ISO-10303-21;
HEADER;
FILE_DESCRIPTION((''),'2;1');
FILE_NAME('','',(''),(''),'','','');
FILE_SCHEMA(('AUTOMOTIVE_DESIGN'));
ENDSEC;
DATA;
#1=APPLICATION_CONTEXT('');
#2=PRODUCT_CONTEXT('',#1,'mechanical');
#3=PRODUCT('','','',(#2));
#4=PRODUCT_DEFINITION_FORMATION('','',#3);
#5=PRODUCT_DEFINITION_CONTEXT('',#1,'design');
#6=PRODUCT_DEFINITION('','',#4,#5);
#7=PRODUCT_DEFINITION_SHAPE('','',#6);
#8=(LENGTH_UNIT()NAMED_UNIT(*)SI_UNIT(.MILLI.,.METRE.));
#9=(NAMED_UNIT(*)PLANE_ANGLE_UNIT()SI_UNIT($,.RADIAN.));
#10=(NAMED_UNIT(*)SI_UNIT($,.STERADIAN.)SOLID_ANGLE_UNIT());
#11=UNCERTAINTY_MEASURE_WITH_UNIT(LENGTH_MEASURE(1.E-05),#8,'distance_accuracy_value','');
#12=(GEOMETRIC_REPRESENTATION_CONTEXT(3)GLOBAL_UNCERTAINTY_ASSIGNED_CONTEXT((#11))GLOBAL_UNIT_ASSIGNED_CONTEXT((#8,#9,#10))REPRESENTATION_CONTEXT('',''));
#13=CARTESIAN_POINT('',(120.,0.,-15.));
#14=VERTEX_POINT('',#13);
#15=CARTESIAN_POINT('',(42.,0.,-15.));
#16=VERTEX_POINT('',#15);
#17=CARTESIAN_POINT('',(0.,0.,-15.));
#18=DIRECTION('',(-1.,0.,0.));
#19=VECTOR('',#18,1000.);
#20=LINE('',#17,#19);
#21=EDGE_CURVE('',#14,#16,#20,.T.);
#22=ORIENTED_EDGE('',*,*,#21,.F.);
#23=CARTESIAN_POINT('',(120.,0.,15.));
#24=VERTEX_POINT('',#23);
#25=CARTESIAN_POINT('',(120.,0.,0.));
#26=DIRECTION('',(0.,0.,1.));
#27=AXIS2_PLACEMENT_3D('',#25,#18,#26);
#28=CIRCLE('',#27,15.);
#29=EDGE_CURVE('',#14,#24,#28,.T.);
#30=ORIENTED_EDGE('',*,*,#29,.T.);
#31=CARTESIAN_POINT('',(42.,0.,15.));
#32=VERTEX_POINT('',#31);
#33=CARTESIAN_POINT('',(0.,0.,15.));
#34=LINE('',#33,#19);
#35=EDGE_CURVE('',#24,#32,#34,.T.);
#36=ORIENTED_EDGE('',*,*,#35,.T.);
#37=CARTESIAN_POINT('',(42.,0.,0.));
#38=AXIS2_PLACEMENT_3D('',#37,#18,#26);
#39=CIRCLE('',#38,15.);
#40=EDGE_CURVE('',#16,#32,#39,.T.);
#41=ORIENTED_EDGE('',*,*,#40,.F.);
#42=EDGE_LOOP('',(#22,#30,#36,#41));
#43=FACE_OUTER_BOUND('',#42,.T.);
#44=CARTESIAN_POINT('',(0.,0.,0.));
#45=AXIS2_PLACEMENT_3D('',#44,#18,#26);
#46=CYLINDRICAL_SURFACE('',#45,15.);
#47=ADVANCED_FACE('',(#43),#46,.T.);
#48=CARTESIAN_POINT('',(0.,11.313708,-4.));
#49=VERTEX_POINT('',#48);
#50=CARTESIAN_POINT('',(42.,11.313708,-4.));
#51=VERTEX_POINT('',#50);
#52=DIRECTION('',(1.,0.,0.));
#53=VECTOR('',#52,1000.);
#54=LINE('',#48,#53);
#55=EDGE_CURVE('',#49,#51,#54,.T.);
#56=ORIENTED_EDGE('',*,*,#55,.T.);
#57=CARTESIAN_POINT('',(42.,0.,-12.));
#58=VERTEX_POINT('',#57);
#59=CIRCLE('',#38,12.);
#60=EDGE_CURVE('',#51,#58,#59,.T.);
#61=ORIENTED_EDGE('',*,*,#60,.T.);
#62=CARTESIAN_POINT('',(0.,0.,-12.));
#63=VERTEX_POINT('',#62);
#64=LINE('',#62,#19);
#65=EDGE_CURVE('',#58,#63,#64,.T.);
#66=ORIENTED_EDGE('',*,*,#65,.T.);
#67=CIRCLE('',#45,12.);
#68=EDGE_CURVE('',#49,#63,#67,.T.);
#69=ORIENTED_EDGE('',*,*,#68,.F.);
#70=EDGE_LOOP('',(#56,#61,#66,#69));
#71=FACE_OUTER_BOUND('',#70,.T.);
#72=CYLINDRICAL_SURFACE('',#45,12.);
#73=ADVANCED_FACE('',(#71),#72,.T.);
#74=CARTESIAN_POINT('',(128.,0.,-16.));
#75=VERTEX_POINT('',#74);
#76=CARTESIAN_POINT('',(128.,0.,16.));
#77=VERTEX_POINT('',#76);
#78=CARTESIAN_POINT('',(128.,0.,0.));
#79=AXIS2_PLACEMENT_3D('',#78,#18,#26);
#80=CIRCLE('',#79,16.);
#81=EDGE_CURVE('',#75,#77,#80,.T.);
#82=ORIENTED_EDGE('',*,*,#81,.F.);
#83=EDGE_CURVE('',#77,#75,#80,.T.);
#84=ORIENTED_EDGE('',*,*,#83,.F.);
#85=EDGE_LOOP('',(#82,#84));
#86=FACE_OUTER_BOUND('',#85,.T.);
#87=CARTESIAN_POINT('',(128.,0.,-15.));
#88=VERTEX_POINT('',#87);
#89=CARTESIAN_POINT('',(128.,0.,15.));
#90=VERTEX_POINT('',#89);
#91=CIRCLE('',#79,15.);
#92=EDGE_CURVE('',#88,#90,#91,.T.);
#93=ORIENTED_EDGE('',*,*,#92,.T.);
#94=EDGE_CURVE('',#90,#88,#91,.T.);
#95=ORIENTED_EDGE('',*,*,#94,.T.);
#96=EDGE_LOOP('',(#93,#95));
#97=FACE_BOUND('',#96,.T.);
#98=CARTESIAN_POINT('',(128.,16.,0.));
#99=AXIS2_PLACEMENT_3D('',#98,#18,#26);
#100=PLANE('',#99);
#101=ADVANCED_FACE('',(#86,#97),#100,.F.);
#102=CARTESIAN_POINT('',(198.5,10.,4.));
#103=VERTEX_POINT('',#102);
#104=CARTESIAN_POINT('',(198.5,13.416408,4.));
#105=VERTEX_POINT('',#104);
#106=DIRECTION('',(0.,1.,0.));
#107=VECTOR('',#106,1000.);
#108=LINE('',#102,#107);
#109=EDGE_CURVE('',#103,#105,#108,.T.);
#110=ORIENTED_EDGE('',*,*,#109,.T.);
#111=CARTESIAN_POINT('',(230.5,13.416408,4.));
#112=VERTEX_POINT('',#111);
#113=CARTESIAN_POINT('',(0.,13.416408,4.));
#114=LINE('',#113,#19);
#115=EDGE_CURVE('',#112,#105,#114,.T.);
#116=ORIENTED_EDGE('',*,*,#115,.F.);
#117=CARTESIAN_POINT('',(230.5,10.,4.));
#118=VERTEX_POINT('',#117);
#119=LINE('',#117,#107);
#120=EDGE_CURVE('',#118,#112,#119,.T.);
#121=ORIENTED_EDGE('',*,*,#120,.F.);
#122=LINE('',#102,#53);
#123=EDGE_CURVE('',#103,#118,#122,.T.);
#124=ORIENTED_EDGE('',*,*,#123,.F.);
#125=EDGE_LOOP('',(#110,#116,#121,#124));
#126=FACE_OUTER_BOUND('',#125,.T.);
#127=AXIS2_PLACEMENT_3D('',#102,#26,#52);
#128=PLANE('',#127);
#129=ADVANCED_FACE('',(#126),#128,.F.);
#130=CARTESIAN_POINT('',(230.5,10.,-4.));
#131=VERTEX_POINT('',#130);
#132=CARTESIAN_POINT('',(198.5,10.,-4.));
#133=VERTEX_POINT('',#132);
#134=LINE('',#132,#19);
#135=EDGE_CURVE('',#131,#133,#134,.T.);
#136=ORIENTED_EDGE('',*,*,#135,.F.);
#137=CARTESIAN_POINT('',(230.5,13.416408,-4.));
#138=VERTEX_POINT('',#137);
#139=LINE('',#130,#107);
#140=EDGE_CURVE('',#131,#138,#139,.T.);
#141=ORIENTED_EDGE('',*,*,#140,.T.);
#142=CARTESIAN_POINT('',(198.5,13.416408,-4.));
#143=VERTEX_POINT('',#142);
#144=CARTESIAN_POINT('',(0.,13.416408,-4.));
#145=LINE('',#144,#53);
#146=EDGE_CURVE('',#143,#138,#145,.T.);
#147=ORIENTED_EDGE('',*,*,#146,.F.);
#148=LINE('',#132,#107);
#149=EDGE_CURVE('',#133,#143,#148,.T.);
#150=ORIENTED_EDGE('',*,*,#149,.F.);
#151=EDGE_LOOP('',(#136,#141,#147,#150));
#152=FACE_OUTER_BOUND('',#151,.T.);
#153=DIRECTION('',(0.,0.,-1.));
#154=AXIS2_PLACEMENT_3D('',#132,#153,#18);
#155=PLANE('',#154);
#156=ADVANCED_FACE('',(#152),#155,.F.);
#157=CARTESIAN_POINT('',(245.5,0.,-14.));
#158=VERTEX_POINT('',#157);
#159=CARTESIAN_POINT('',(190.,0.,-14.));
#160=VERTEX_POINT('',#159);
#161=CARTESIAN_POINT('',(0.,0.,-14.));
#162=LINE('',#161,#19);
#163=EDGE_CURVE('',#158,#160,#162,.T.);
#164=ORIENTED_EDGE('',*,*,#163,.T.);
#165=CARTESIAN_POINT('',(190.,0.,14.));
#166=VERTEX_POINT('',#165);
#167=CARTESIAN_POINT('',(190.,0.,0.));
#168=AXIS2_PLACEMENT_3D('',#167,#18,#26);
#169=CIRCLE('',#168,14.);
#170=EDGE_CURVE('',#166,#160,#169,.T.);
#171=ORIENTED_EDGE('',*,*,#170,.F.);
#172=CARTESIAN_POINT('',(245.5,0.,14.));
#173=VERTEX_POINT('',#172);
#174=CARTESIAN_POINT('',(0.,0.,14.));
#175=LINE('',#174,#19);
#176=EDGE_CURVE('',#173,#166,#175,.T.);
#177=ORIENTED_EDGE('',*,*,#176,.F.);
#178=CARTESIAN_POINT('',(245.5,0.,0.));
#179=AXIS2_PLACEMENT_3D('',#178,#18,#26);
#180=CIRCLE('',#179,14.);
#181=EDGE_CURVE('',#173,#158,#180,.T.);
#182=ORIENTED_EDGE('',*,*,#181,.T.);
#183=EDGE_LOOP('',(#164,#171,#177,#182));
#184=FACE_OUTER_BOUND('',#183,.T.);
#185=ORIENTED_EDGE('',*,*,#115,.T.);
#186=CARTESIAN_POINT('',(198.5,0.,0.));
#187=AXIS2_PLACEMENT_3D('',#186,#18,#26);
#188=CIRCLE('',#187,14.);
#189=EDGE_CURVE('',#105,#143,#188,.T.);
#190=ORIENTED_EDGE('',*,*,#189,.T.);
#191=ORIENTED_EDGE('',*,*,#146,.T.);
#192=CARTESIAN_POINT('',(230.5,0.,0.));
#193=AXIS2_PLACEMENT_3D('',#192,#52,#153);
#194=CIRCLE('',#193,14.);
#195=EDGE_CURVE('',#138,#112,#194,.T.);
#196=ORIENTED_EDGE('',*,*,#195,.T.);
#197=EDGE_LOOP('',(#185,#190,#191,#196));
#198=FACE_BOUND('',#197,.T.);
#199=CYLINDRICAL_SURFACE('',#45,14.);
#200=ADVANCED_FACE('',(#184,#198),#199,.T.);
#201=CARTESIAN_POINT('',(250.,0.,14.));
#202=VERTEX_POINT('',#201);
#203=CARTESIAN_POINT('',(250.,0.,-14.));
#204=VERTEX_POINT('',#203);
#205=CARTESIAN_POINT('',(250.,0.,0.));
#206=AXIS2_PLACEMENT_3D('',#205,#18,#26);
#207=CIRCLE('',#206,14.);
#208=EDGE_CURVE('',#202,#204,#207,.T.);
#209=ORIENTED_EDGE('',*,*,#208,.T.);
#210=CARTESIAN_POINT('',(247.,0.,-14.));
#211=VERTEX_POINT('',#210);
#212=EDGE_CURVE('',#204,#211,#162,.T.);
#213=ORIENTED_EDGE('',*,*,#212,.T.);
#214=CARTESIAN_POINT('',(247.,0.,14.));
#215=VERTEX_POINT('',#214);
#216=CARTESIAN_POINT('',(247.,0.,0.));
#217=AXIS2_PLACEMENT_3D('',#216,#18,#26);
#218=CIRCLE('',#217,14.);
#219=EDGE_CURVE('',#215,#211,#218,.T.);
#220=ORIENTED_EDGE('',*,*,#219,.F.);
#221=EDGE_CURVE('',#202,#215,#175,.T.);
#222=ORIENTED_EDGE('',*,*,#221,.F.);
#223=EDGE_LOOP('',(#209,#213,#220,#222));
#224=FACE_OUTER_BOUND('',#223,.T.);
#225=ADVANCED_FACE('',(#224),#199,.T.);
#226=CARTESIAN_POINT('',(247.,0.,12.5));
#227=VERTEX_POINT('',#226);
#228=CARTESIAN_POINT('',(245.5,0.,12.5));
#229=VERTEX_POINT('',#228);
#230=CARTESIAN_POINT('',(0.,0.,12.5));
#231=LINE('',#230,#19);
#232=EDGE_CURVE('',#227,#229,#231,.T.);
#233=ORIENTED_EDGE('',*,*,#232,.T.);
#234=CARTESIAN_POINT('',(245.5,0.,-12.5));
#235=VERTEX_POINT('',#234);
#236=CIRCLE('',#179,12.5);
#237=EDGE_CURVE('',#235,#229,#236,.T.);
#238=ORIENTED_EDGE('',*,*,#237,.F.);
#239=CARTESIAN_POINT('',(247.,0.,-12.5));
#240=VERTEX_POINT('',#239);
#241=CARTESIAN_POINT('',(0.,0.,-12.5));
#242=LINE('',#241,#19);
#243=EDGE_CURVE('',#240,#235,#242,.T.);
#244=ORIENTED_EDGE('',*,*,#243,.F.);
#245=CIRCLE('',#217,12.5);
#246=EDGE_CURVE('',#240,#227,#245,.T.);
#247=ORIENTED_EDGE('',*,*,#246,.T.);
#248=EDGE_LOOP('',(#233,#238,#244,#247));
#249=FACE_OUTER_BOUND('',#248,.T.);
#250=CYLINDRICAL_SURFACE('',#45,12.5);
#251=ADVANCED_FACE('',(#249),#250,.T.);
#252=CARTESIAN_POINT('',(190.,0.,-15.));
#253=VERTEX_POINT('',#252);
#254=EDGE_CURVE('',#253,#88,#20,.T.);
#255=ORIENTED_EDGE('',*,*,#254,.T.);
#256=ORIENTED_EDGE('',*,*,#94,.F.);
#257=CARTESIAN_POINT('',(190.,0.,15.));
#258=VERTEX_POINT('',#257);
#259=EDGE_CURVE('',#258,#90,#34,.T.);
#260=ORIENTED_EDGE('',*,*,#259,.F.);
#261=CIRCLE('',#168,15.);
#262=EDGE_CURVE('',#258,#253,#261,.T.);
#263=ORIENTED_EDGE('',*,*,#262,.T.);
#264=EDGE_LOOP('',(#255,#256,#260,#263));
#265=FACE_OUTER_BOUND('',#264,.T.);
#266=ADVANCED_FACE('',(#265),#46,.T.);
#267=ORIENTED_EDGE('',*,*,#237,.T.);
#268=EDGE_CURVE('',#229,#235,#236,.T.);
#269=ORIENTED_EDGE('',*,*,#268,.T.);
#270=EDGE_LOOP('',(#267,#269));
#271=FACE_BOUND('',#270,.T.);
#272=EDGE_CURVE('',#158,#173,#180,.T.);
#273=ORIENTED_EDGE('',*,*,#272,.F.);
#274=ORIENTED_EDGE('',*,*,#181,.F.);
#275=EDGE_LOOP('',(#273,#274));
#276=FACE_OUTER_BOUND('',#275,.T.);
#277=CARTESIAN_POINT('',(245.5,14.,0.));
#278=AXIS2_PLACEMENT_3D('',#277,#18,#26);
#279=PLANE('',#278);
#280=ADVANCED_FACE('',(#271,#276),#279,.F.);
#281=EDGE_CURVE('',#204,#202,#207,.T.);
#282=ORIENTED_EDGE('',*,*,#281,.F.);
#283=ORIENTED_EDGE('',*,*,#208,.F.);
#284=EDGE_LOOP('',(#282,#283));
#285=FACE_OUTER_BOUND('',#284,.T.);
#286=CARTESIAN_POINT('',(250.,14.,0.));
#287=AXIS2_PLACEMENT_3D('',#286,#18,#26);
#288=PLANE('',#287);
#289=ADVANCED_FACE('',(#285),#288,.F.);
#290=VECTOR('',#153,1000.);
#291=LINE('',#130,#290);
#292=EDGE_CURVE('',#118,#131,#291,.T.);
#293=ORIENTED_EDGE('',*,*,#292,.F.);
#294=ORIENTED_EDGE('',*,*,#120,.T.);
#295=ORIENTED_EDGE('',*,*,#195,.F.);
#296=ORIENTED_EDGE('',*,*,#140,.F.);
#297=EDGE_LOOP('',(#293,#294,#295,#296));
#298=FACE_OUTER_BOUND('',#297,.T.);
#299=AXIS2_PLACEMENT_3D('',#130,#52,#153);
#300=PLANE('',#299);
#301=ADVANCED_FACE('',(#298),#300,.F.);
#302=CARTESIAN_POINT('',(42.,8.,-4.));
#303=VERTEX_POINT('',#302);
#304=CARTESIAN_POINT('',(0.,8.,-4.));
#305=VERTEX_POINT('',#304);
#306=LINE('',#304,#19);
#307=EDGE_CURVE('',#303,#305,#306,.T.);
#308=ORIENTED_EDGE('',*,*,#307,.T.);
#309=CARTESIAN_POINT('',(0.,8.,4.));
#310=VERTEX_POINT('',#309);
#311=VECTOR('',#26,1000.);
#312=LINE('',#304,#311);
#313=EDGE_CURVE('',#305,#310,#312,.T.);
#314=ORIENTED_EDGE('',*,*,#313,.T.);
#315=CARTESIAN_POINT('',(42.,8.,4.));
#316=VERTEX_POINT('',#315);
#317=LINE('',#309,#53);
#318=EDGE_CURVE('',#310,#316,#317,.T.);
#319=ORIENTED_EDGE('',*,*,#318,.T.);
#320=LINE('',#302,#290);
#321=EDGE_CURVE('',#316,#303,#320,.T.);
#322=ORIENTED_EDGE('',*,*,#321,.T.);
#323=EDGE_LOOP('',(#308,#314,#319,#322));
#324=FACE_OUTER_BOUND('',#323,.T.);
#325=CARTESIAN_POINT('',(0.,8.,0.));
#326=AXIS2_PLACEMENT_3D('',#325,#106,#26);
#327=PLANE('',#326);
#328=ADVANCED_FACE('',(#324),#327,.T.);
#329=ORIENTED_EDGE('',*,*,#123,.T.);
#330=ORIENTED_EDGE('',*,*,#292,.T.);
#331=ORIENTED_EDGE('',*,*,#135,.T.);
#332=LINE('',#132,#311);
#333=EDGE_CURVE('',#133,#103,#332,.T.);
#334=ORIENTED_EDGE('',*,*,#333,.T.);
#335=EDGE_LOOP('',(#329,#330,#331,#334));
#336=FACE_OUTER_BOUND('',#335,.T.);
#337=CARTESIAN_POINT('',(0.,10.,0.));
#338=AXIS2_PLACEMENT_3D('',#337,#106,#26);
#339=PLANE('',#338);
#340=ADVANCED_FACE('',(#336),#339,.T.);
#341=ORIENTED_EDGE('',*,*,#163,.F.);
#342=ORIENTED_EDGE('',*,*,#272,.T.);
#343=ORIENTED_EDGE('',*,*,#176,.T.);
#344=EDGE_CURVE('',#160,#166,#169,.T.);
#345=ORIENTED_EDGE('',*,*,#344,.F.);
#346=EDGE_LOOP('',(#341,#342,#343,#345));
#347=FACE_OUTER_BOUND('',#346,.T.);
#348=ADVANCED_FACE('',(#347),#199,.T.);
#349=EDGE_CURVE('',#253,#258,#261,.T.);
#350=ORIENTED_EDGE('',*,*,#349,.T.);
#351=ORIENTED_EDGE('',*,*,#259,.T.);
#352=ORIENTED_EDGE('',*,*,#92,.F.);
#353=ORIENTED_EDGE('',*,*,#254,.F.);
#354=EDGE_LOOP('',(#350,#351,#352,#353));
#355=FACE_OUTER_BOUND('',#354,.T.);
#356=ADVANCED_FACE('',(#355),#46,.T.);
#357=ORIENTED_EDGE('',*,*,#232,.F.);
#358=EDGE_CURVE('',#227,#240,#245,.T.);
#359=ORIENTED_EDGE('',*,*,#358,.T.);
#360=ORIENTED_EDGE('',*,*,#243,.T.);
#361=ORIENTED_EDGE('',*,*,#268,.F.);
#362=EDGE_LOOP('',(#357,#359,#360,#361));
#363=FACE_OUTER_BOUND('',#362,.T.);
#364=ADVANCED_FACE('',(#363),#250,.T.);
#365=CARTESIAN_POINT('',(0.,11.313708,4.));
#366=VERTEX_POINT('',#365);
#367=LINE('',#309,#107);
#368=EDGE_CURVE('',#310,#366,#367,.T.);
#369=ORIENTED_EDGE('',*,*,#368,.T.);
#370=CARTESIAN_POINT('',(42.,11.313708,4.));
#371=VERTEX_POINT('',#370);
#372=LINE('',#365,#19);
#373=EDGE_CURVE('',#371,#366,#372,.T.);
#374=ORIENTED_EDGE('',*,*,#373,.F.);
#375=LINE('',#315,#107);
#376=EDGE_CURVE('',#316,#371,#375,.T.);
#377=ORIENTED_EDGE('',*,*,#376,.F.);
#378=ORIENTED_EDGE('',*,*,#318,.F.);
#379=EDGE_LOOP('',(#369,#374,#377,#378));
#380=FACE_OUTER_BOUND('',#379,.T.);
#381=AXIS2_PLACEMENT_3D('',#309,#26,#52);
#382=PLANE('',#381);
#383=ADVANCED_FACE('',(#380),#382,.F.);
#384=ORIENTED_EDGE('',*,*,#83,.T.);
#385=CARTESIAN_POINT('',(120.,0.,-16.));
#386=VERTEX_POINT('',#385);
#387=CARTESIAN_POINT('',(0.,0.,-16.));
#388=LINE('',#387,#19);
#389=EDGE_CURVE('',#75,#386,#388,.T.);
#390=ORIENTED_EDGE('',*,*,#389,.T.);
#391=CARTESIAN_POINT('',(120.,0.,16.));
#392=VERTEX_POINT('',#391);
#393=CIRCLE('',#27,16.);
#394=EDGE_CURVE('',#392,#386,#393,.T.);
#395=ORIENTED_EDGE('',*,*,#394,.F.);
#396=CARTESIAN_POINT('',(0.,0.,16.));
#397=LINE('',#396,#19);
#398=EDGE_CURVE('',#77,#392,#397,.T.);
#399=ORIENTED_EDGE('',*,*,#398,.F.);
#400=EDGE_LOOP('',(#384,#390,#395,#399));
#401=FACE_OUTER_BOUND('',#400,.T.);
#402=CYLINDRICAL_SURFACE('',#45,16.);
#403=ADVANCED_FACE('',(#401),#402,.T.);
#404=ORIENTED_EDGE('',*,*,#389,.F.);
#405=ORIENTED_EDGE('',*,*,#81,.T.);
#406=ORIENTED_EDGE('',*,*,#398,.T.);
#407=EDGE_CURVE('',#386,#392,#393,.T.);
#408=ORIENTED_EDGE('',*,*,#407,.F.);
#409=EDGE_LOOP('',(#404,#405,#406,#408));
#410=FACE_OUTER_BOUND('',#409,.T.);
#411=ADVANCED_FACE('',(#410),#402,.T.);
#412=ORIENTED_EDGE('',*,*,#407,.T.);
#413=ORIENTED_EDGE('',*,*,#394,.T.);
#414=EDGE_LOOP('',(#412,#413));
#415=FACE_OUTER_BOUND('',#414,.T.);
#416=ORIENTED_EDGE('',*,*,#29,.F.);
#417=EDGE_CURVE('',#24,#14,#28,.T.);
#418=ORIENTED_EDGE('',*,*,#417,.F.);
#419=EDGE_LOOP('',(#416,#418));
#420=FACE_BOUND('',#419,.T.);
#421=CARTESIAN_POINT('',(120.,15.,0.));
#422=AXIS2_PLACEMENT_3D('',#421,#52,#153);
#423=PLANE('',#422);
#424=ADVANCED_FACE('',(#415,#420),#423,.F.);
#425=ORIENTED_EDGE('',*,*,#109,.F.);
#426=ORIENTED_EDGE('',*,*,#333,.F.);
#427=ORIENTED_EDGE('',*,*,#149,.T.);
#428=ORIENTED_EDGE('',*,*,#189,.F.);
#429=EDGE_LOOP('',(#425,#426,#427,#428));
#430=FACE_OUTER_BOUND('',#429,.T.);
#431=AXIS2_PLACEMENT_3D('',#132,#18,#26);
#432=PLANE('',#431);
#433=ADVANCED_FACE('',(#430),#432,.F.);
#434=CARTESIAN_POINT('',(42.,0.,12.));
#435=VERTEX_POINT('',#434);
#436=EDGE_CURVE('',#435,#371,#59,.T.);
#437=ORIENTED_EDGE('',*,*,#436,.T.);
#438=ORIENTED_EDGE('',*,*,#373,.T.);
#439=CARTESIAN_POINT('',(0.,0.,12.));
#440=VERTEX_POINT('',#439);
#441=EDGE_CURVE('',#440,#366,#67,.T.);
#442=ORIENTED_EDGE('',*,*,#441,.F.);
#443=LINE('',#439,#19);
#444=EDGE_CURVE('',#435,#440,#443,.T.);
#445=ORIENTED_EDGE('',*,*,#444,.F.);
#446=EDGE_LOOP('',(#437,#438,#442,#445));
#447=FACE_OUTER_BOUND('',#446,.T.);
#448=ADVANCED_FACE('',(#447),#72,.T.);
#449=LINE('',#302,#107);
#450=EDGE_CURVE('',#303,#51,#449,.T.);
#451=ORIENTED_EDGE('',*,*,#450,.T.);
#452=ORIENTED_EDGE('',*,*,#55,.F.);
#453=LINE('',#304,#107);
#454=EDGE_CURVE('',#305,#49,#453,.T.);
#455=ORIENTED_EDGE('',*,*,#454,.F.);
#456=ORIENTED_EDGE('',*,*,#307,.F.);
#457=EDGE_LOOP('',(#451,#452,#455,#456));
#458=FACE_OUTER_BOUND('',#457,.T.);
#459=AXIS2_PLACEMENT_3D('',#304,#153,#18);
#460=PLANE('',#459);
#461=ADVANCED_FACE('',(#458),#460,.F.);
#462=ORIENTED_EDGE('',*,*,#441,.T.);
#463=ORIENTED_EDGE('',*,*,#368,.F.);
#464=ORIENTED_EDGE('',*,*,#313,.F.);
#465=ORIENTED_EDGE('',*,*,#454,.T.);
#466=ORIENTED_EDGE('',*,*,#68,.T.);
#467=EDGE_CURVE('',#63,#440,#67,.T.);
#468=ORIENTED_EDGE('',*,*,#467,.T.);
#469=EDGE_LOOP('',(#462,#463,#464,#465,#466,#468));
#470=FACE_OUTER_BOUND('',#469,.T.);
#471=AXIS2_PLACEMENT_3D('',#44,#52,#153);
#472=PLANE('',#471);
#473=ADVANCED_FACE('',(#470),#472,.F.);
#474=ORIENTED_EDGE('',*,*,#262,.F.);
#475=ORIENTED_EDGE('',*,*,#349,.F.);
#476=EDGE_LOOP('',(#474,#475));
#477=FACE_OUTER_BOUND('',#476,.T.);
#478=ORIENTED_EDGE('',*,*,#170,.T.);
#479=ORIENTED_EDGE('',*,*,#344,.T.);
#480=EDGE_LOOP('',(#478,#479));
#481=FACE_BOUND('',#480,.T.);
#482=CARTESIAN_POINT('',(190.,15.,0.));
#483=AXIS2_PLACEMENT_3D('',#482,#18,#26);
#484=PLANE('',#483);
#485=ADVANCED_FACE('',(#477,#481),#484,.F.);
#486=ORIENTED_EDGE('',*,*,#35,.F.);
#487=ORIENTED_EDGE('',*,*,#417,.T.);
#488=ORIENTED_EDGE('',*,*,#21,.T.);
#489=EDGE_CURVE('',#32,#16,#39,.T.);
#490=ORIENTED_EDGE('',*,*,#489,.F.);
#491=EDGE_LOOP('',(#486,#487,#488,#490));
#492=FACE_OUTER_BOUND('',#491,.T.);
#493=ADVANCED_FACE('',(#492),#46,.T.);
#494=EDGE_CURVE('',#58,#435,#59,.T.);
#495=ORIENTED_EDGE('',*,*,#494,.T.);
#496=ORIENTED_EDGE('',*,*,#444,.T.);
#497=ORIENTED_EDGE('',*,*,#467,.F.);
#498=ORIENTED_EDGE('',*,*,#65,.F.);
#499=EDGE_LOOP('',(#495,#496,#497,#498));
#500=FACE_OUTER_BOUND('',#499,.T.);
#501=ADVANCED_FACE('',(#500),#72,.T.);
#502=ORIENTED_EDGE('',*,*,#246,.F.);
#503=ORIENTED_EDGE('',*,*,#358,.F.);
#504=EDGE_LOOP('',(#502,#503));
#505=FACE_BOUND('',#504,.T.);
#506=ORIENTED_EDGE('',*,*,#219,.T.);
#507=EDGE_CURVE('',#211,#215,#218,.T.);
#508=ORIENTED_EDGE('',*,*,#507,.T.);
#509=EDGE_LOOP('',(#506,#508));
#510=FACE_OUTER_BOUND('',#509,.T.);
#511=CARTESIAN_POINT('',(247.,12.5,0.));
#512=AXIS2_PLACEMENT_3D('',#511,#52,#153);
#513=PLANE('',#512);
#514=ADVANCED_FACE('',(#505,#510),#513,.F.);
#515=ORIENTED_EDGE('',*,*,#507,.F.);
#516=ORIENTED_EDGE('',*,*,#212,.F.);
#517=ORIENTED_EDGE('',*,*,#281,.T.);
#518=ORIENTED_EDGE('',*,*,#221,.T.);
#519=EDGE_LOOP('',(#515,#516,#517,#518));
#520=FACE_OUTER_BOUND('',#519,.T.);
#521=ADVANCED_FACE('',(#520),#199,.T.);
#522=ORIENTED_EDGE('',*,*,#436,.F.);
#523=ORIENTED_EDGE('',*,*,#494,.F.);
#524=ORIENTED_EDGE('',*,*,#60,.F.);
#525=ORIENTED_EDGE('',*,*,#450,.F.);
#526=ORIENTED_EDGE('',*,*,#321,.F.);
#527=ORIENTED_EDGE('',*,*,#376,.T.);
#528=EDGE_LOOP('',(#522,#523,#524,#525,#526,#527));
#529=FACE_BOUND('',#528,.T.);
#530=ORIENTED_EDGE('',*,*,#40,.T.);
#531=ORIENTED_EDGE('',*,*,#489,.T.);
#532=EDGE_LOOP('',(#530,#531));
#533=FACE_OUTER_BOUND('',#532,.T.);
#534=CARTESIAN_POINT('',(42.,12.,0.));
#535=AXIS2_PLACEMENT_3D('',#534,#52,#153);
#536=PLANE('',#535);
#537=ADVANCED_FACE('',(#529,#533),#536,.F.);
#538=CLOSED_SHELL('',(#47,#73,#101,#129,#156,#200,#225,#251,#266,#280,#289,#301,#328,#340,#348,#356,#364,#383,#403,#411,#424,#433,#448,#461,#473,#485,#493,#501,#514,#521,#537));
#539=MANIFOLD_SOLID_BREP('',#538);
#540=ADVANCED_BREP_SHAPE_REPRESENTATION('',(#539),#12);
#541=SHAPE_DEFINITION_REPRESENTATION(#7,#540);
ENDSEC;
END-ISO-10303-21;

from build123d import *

# Parameters (mm, degrees)
KEYWAY_1_SKETCH_W  = 42
KEYWAY_1_SKETCH_H  = 8
KEYWAY_1_CUT_DEPTH = 4
KEYWAY_2_SKETCH_W  = 32
KEYWAY_2_SKETCH_H  = 8
KEYWAY_2_CUT_DEPTH = 4


with BuildPart() as part:
    # Shaft Profile Sketch → Stepped Shaft Body (revolve)
    with BuildSketch(Plane.XY, mode=Mode.PRIVATE) as stepped_shaft_body_sk:
        Polygon((0, 0), (0, 12), (42, 12), (42, 15), (120, 15), (120, 16), (128, 16), (128, 15), (190, 15), (190, 14), (245.5, 14), (245.5, 12.5), (247, 12.5), (247, 14), (250, 14), (250, 0), align=None)
    revolve(stepped_shaft_body_sk.sketch.rotate(Axis((0, 0, 0), (1, 0, 0)), 90), axis=Axis((0, 0, 0), (1, 0, 0)))

    # Keyway 1 Sketch → Keyway 1 Cut (cut)
    with BuildSketch(Plane(origin=(0, 12, 0), x_dir=(1, 0, 0), z_dir=(0, 1, 0))):
        with Locations((21, 0)):
            Rectangle(KEYWAY_1_SKETCH_W, KEYWAY_1_SKETCH_H)
    extrude(amount=-KEYWAY_1_CUT_DEPTH, mode=Mode.SUBTRACT)

    # Keyway 2 Sketch → Keyway 2 Cut (cut)
    with BuildSketch(Plane(origin=(0, 14, 0), x_dir=(1, 0, 0), z_dir=(0, 1, 0))):
        with Locations((214.5, 0)):
            Rectangle(KEYWAY_2_SKETCH_W, KEYWAY_2_SKETCH_H)
    extrude(amount=-KEYWAY_2_CUT_DEPTH, mode=Mode.SUBTRACT)


solid = part.part
